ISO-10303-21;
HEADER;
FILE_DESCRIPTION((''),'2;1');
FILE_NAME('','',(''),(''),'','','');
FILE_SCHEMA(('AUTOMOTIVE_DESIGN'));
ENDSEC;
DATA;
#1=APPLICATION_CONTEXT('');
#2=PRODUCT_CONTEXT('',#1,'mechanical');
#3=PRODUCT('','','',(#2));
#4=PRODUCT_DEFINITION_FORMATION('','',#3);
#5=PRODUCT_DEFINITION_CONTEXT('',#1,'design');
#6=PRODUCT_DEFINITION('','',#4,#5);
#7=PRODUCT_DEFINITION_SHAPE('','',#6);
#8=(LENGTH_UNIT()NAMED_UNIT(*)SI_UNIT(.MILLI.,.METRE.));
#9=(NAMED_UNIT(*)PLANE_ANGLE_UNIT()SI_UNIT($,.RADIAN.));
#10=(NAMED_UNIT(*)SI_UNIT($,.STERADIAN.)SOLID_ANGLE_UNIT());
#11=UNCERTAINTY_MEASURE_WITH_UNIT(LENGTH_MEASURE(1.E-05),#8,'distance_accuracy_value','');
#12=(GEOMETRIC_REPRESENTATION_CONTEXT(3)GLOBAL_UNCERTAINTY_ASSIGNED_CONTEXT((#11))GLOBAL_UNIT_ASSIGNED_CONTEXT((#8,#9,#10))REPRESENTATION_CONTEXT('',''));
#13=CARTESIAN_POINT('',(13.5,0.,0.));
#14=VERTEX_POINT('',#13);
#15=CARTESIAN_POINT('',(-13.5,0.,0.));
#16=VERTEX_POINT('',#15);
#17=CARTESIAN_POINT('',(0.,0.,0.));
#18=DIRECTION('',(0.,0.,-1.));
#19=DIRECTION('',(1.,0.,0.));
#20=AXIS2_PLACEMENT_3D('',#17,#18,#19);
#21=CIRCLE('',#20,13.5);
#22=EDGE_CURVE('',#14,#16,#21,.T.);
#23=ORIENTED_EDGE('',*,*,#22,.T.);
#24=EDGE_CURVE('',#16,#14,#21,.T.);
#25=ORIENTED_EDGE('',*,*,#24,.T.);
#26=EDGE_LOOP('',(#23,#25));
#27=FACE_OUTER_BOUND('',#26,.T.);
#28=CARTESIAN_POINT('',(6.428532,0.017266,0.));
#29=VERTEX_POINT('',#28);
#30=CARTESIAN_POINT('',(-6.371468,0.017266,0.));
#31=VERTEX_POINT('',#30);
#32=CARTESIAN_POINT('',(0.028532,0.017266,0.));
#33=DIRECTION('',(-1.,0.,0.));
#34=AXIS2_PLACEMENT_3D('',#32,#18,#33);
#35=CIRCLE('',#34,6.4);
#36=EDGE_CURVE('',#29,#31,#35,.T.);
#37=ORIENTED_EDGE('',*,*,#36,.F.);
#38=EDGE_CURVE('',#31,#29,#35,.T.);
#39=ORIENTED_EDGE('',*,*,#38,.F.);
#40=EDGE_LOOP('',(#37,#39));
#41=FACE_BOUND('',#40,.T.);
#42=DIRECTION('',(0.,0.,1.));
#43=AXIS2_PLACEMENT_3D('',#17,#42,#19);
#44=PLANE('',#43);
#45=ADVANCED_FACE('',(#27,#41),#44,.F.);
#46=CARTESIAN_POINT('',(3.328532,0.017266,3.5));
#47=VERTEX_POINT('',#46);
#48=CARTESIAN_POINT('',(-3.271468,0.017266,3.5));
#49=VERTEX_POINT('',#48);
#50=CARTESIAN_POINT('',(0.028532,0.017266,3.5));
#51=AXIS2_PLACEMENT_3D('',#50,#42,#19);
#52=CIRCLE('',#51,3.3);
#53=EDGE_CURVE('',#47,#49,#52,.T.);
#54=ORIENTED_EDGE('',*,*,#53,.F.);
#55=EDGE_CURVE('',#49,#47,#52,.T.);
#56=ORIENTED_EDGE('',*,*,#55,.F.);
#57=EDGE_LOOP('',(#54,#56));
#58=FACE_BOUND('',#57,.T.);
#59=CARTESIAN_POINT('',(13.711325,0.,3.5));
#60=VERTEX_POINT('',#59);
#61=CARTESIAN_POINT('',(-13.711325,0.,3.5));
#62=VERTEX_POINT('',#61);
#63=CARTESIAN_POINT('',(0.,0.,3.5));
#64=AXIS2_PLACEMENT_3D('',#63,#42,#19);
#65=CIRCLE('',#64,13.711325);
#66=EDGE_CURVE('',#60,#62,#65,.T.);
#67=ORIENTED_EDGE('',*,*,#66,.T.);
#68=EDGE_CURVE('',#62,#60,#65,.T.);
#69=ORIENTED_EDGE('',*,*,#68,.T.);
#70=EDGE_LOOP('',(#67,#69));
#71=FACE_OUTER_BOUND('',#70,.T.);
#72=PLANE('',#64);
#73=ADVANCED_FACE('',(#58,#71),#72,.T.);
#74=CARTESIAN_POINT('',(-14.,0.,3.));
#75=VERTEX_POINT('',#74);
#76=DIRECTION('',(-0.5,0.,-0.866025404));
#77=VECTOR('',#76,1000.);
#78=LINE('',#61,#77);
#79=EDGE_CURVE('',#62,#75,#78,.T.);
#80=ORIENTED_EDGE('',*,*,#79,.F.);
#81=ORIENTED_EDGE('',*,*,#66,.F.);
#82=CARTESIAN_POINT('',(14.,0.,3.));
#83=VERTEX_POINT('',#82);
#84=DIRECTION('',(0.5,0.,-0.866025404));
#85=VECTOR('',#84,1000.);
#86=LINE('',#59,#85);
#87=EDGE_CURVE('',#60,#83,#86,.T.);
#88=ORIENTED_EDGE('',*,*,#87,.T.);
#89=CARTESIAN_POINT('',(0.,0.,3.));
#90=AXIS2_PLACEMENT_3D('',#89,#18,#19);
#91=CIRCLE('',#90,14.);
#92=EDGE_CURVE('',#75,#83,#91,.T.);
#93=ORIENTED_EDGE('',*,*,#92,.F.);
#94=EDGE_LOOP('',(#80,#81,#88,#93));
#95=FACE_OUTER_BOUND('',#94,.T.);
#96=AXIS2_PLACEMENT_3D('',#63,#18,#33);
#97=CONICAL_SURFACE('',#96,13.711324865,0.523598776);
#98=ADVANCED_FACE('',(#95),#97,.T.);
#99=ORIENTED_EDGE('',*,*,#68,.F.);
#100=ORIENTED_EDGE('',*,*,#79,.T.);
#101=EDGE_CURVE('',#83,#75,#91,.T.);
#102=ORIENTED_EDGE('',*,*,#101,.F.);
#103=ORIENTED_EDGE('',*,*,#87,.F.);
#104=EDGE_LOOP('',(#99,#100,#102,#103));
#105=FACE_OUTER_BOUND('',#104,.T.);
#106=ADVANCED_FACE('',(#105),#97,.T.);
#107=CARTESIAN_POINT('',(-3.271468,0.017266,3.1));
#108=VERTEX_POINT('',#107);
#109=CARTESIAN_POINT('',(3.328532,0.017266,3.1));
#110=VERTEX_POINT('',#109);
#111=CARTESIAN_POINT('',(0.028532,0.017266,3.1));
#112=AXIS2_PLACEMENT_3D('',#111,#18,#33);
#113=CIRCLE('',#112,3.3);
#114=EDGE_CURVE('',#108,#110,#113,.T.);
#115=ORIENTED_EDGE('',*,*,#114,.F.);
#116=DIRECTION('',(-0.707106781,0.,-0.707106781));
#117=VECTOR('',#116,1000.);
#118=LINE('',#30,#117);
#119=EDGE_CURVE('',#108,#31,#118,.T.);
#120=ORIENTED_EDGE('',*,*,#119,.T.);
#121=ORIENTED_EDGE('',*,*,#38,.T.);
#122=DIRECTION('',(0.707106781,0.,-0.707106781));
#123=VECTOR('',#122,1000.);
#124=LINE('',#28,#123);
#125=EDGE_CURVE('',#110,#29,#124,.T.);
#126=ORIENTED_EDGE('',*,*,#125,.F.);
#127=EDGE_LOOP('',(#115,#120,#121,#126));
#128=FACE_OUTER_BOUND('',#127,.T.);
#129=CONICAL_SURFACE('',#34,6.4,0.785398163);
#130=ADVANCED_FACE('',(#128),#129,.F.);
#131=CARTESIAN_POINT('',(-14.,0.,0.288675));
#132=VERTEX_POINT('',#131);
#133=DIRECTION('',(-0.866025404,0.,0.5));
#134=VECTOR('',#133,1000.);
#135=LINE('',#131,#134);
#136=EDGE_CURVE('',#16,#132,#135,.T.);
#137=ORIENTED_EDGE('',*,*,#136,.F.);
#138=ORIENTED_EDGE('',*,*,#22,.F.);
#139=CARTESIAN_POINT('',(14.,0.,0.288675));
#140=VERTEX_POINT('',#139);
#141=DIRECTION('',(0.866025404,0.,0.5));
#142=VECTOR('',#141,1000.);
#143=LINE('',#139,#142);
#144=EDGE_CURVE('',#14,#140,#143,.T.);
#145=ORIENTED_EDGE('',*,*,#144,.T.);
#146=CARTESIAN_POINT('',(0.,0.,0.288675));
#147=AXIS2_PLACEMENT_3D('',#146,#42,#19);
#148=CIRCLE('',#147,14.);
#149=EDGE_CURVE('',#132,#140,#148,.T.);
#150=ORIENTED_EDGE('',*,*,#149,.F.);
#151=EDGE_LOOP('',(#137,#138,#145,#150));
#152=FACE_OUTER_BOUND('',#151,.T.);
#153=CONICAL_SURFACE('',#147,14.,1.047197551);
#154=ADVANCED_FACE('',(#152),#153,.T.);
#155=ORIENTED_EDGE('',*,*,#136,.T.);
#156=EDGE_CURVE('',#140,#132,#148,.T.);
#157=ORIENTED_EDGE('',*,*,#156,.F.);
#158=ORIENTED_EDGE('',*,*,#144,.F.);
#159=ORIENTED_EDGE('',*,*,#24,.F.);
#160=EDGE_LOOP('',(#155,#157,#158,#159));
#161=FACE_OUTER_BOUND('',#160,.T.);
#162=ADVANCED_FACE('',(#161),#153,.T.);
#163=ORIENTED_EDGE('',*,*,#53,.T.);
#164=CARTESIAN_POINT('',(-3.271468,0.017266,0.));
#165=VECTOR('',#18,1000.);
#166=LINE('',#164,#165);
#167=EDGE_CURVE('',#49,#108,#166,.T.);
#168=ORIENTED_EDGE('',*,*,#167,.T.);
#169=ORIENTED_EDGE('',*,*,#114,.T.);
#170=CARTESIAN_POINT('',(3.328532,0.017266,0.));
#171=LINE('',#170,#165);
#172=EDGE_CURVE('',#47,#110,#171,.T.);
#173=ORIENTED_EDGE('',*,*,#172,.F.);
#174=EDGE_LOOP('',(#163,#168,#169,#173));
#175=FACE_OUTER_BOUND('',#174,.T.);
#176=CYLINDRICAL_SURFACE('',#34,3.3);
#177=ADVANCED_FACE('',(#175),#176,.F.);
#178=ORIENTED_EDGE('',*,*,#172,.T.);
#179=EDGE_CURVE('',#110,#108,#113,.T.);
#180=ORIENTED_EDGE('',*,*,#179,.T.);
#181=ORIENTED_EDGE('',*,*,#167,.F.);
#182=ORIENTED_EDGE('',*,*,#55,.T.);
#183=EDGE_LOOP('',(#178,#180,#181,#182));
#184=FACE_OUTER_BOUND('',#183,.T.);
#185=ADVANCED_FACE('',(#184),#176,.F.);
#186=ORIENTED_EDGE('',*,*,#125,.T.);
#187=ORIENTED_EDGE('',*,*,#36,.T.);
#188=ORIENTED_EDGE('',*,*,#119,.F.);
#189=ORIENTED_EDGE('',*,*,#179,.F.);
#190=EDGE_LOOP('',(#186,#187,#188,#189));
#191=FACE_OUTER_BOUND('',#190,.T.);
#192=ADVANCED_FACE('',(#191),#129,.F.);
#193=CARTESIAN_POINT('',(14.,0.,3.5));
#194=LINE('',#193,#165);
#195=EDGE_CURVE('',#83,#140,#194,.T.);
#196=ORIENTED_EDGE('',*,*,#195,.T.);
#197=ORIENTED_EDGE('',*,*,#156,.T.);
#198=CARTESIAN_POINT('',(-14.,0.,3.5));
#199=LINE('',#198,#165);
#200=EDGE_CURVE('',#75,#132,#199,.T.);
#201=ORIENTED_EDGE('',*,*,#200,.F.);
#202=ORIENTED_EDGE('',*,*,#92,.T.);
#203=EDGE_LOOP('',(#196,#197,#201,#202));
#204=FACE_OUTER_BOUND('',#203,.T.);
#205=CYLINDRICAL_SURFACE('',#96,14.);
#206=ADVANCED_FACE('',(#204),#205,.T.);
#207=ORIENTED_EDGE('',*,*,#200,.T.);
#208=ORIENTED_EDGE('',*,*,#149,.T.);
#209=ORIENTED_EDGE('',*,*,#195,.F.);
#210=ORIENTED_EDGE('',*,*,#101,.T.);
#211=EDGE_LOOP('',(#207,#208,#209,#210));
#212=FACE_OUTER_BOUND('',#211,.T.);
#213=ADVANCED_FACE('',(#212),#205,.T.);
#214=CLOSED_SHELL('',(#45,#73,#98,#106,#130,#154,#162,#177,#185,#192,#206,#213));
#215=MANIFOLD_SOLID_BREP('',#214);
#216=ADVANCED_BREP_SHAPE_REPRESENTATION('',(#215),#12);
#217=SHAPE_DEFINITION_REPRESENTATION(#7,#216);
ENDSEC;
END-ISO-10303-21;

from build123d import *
from OCP.BRepFilletAPI import BRepFilletAPI_MakeChamfer

# Parameters (mm, degrees)
SKETCH1_R                                            = 14
BOSS_EXTRUDE1_DEPTH                                  = 3.5
CHAMFER1_SIZE                                        = 0.5
CHAMFER1_SIZE2                                       = 0.288675135
CSK_FOR_M6_HEXAGON_LOBULAR_SOCKET_RAISED_D           = 6.6
CSK_FOR_M6_HEXAGON_LOBULAR_SOCKET_RAISED_DEPTH       = 6.5
CSK_FOR_M6_HEXAGON_LOBULAR_SOCKET_RAISED_CSINK_D     = 12.8
CSK_FOR_M6_HEXAGON_LOBULAR_SOCKET_RAISED_CSINK_ANGLE = 90
CSK_FOR_M6_HEXAGON_LOBULAR_SOCKET_RAISED_TIP         = 1.982840043


with BuildPart() as part:
    # Sketch1 → Boss-Extrude1 (new body)
    with BuildSketch(Plane.XY):
        Circle(SKETCH1_R)
    extrude(amount=BOSS_EXTRUDE1_DEPTH)

    # Chamfer1: one chamfer whose edges measure the first distance from different faces: ONE call of the kernel's chamfer builder (chamfer() names one face for all edges)
    chamfer1_edges_1 = [part.edges().sort_by_distance(p)[0] for p in [
        (-14, 0, 0),
    ]]
    chamfer1_side_1 = [part.faces().sort_by_distance(p)[0] for p in [
        (0, 0, 0),
    ]]
    chamfer1_edges_2 = [part.edges().sort_by_distance(p)[0] for p in [
        (-14, 0, 3.5),
    ]]
    chamfer1_side_2 = [part.faces().sort_by_distance(p)[0] for p in [
        (-14, 0, 1.75),
    ]]
    chamfer1 = BRepFilletAPI_MakeChamfer(part.part.solid().wrapped)
    for e in chamfer1_edges_1:
        chamfer1.Add(CHAMFER1_SIZE, CHAMFER1_SIZE2, e.wrapped, chamfer1_side_1[0].wrapped)  # the first distance lies on this face
    for e in chamfer1_edges_2:
        chamfer1.Add(CHAMFER1_SIZE, CHAMFER1_SIZE2, e.wrapped, chamfer1_side_2[0].wrapped)  # the first distance lies on this face
    add(Compound.cast(chamfer1.Shape()), mode=Mode.REPLACE)

    # CSK for M6 Hexagon lobular socket raised CTSK head screws1
    with Locations(Plane(origin=(0.028531749, 0.017266162, 0), x_dir=(-1, 0, 0), z_dir=(0, 0, -1))):
        with Locations((0, 0)):
            CounterSinkHole(CSK_FOR_M6_HEXAGON_LOBULAR_SOCKET_RAISED_D / 2, CSK_FOR_M6_HEXAGON_LOBULAR_SOCKET_RAISED_CSINK_D / 2, depth=CSK_FOR_M6_HEXAGON_LOBULAR_SOCKET_RAISED_DEPTH, counter_sink_angle=CSK_FOR_M6_HEXAGON_LOBULAR_SOCKET_RAISED_CSINK_ANGLE)
            with Locations((0, 0, -(CSK_FOR_M6_HEXAGON_LOBULAR_SOCKET_RAISED_DEPTH + CSK_FOR_M6_HEXAGON_LOBULAR_SOCKET_RAISED_TIP / 2))):  # 118° drill point
                Cone(0, CSK_FOR_M6_HEXAGON_LOBULAR_SOCKET_RAISED_D / 2, CSK_FOR_M6_HEXAGON_LOBULAR_SOCKET_RAISED_TIP, mode=Mode.SUBTRACT)


solid = part.part
